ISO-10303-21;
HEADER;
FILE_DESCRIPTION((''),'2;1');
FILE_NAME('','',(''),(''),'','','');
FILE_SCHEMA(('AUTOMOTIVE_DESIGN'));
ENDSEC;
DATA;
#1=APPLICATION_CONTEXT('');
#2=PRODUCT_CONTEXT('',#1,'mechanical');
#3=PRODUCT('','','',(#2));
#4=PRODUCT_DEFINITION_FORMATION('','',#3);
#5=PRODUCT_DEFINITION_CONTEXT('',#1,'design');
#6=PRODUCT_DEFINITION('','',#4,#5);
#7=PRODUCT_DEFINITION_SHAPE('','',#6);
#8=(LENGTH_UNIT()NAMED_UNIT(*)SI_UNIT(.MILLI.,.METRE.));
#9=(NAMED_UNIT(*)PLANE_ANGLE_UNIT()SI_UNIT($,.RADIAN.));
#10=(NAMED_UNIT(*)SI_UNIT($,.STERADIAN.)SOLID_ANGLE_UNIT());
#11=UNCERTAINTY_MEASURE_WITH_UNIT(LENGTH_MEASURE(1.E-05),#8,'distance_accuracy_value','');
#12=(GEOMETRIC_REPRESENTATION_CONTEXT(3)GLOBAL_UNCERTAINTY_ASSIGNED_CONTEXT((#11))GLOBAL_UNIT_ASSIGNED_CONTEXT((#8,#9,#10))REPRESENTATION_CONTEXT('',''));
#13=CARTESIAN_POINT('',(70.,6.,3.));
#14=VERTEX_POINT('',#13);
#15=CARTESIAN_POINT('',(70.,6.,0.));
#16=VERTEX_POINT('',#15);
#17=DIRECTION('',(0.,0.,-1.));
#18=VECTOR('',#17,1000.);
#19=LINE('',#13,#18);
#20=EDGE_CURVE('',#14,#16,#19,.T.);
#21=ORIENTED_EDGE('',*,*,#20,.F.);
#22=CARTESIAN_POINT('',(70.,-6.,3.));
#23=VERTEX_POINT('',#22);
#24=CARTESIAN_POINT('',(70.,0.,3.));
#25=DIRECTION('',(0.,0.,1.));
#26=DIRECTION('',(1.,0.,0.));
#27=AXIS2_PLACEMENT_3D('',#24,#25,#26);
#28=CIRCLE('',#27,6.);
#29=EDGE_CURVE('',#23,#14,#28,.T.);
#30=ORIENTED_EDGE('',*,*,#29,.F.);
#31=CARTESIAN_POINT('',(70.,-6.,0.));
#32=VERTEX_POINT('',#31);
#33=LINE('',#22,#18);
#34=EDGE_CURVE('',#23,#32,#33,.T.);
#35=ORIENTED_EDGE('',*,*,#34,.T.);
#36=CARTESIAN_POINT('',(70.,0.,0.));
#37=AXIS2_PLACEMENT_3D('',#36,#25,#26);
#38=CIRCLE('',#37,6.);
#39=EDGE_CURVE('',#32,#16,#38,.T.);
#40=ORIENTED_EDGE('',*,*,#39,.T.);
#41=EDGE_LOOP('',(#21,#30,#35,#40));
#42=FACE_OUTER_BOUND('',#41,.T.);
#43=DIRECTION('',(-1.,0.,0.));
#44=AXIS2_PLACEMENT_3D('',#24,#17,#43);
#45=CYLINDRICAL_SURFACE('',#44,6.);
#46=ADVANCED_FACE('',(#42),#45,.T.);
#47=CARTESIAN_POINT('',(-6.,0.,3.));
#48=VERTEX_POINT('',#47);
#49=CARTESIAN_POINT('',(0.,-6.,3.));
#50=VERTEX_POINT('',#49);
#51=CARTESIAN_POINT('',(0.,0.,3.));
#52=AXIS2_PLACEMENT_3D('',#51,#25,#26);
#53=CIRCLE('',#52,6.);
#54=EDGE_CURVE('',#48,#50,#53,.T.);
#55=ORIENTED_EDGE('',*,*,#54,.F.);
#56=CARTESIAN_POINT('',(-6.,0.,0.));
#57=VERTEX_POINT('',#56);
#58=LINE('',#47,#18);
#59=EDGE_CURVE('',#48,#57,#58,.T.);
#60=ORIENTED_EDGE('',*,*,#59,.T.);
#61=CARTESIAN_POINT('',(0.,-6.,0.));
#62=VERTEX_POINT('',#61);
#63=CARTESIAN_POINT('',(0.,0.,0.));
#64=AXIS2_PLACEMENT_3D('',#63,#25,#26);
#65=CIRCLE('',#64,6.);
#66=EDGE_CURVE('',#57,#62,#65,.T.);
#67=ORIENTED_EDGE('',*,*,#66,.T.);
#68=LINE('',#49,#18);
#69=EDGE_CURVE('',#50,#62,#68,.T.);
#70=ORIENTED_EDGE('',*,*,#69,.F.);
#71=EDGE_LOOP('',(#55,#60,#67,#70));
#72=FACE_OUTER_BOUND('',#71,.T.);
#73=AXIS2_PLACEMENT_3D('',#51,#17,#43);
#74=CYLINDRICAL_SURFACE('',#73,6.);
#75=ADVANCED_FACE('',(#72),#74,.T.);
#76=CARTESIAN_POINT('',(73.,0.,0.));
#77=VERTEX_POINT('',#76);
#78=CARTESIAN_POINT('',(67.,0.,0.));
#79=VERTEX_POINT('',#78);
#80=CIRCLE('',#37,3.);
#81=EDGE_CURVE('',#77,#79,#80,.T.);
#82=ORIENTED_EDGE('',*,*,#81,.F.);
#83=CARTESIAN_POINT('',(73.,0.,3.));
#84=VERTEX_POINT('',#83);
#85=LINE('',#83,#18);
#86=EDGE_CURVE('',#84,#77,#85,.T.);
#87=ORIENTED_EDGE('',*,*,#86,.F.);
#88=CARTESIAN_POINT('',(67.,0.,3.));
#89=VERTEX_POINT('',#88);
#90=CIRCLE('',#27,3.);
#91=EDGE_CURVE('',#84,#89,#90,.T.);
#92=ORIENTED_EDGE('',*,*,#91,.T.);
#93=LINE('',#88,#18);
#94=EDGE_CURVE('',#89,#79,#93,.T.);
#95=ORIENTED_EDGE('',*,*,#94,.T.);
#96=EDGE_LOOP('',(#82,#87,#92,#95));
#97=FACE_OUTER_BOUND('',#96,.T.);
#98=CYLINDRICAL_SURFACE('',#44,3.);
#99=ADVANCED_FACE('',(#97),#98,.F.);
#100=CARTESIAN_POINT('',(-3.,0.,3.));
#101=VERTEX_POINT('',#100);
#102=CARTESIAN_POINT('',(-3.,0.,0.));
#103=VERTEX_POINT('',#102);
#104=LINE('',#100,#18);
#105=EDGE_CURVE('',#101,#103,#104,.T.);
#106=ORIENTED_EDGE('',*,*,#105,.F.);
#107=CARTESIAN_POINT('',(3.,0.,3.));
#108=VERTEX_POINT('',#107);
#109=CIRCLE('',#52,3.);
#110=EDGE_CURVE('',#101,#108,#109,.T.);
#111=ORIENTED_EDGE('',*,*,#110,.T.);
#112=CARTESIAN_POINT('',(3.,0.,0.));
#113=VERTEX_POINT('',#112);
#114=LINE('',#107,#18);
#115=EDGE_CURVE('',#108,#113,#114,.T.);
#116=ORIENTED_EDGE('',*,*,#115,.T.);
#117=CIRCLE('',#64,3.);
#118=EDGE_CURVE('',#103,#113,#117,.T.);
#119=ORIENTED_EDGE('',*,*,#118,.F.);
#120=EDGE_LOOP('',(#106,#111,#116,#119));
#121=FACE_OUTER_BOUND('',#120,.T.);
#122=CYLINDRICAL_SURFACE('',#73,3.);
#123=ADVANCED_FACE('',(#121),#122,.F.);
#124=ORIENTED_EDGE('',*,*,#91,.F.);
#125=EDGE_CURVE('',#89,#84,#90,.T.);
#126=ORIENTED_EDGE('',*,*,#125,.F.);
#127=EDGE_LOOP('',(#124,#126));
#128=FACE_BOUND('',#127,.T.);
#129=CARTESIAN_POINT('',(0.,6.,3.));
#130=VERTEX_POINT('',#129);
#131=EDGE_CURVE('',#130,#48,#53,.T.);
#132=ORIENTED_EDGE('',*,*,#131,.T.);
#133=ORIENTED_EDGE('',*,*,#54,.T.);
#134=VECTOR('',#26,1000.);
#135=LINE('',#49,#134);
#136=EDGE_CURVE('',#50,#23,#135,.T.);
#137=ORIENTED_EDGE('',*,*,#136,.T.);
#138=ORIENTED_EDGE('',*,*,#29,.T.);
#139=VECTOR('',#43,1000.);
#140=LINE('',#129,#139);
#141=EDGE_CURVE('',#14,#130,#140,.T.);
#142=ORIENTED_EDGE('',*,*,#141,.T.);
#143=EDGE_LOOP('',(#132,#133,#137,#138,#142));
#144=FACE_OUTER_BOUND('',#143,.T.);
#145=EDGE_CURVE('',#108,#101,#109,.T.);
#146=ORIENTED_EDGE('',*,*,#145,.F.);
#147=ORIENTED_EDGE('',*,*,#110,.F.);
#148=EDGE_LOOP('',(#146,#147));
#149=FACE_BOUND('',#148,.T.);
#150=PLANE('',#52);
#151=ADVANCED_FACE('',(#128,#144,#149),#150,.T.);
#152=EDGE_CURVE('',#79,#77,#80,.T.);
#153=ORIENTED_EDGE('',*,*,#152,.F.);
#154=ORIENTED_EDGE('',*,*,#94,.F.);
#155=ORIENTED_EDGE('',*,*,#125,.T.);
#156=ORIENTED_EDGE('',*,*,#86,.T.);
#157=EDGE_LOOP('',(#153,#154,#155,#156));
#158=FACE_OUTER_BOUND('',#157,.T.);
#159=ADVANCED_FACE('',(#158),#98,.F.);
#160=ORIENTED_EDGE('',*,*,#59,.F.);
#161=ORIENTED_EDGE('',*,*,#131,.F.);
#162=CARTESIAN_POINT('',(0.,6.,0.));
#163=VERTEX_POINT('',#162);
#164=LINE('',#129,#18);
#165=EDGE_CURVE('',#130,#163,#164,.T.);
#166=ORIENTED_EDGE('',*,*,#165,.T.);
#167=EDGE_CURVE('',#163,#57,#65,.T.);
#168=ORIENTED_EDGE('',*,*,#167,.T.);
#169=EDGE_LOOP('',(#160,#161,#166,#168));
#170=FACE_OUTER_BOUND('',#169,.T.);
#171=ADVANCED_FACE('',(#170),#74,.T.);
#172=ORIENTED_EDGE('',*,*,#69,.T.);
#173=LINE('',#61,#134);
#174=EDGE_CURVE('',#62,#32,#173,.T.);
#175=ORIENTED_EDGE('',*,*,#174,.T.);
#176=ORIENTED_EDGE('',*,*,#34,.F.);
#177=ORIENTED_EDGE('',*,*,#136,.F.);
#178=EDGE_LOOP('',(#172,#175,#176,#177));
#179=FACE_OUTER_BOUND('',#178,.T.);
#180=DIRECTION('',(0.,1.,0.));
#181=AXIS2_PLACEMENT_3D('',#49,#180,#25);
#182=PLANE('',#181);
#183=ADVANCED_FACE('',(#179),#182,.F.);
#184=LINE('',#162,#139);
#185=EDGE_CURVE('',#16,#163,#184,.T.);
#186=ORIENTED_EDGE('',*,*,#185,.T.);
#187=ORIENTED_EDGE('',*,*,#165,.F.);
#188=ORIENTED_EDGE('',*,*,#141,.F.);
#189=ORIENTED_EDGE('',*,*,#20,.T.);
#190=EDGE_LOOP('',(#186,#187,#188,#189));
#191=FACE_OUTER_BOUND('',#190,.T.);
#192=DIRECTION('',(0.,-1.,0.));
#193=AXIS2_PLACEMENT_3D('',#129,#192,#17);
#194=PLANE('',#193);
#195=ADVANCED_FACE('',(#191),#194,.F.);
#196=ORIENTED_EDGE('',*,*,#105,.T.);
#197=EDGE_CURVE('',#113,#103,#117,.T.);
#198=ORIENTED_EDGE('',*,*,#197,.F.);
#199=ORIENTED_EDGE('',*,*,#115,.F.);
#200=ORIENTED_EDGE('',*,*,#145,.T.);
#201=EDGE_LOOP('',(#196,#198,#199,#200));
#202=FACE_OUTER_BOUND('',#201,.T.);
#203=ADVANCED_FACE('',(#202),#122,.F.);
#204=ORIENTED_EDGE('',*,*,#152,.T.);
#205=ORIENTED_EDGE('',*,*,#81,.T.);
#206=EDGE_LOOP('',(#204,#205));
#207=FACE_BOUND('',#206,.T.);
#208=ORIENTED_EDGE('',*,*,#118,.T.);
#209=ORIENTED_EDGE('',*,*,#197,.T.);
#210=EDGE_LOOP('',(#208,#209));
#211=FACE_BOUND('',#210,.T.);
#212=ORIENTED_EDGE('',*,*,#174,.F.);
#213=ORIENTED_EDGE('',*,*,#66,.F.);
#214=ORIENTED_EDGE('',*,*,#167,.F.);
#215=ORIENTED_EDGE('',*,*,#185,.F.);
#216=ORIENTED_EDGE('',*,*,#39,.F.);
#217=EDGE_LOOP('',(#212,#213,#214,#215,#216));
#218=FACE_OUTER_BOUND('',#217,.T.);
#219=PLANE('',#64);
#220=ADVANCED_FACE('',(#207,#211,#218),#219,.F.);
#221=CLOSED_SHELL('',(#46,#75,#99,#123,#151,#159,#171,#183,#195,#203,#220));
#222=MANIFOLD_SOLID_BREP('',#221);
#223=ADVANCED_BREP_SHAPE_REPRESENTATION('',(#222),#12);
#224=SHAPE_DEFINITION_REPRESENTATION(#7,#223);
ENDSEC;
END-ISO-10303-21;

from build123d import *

# Parameters (mm, degrees)
SKETCH1_R           = 3
BOSS_EXTRUDE1_DEPTH = 3


with BuildPart() as part:
    # Sketch1 → Boss-Extrude1 (new body)
    with BuildSketch(Plane.XY):
        with BuildLine():
            Line((0, 6), (70, 6))
            ThreePointArc((70, 6), (76, 0), (70, -6))
            Line((70, -6), (0, -6))
            ThreePointArc((0, -6), (-6, 0), (0, 6))
        make_face()
        Circle(SKETCH1_R, mode=Mode.SUBTRACT)
        with Locations((70, 0)):
            Circle(SKETCH1_R, mode=Mode.SUBTRACT)
    extrude(amount=BOSS_EXTRUDE1_DEPTH)


solid = part.part
